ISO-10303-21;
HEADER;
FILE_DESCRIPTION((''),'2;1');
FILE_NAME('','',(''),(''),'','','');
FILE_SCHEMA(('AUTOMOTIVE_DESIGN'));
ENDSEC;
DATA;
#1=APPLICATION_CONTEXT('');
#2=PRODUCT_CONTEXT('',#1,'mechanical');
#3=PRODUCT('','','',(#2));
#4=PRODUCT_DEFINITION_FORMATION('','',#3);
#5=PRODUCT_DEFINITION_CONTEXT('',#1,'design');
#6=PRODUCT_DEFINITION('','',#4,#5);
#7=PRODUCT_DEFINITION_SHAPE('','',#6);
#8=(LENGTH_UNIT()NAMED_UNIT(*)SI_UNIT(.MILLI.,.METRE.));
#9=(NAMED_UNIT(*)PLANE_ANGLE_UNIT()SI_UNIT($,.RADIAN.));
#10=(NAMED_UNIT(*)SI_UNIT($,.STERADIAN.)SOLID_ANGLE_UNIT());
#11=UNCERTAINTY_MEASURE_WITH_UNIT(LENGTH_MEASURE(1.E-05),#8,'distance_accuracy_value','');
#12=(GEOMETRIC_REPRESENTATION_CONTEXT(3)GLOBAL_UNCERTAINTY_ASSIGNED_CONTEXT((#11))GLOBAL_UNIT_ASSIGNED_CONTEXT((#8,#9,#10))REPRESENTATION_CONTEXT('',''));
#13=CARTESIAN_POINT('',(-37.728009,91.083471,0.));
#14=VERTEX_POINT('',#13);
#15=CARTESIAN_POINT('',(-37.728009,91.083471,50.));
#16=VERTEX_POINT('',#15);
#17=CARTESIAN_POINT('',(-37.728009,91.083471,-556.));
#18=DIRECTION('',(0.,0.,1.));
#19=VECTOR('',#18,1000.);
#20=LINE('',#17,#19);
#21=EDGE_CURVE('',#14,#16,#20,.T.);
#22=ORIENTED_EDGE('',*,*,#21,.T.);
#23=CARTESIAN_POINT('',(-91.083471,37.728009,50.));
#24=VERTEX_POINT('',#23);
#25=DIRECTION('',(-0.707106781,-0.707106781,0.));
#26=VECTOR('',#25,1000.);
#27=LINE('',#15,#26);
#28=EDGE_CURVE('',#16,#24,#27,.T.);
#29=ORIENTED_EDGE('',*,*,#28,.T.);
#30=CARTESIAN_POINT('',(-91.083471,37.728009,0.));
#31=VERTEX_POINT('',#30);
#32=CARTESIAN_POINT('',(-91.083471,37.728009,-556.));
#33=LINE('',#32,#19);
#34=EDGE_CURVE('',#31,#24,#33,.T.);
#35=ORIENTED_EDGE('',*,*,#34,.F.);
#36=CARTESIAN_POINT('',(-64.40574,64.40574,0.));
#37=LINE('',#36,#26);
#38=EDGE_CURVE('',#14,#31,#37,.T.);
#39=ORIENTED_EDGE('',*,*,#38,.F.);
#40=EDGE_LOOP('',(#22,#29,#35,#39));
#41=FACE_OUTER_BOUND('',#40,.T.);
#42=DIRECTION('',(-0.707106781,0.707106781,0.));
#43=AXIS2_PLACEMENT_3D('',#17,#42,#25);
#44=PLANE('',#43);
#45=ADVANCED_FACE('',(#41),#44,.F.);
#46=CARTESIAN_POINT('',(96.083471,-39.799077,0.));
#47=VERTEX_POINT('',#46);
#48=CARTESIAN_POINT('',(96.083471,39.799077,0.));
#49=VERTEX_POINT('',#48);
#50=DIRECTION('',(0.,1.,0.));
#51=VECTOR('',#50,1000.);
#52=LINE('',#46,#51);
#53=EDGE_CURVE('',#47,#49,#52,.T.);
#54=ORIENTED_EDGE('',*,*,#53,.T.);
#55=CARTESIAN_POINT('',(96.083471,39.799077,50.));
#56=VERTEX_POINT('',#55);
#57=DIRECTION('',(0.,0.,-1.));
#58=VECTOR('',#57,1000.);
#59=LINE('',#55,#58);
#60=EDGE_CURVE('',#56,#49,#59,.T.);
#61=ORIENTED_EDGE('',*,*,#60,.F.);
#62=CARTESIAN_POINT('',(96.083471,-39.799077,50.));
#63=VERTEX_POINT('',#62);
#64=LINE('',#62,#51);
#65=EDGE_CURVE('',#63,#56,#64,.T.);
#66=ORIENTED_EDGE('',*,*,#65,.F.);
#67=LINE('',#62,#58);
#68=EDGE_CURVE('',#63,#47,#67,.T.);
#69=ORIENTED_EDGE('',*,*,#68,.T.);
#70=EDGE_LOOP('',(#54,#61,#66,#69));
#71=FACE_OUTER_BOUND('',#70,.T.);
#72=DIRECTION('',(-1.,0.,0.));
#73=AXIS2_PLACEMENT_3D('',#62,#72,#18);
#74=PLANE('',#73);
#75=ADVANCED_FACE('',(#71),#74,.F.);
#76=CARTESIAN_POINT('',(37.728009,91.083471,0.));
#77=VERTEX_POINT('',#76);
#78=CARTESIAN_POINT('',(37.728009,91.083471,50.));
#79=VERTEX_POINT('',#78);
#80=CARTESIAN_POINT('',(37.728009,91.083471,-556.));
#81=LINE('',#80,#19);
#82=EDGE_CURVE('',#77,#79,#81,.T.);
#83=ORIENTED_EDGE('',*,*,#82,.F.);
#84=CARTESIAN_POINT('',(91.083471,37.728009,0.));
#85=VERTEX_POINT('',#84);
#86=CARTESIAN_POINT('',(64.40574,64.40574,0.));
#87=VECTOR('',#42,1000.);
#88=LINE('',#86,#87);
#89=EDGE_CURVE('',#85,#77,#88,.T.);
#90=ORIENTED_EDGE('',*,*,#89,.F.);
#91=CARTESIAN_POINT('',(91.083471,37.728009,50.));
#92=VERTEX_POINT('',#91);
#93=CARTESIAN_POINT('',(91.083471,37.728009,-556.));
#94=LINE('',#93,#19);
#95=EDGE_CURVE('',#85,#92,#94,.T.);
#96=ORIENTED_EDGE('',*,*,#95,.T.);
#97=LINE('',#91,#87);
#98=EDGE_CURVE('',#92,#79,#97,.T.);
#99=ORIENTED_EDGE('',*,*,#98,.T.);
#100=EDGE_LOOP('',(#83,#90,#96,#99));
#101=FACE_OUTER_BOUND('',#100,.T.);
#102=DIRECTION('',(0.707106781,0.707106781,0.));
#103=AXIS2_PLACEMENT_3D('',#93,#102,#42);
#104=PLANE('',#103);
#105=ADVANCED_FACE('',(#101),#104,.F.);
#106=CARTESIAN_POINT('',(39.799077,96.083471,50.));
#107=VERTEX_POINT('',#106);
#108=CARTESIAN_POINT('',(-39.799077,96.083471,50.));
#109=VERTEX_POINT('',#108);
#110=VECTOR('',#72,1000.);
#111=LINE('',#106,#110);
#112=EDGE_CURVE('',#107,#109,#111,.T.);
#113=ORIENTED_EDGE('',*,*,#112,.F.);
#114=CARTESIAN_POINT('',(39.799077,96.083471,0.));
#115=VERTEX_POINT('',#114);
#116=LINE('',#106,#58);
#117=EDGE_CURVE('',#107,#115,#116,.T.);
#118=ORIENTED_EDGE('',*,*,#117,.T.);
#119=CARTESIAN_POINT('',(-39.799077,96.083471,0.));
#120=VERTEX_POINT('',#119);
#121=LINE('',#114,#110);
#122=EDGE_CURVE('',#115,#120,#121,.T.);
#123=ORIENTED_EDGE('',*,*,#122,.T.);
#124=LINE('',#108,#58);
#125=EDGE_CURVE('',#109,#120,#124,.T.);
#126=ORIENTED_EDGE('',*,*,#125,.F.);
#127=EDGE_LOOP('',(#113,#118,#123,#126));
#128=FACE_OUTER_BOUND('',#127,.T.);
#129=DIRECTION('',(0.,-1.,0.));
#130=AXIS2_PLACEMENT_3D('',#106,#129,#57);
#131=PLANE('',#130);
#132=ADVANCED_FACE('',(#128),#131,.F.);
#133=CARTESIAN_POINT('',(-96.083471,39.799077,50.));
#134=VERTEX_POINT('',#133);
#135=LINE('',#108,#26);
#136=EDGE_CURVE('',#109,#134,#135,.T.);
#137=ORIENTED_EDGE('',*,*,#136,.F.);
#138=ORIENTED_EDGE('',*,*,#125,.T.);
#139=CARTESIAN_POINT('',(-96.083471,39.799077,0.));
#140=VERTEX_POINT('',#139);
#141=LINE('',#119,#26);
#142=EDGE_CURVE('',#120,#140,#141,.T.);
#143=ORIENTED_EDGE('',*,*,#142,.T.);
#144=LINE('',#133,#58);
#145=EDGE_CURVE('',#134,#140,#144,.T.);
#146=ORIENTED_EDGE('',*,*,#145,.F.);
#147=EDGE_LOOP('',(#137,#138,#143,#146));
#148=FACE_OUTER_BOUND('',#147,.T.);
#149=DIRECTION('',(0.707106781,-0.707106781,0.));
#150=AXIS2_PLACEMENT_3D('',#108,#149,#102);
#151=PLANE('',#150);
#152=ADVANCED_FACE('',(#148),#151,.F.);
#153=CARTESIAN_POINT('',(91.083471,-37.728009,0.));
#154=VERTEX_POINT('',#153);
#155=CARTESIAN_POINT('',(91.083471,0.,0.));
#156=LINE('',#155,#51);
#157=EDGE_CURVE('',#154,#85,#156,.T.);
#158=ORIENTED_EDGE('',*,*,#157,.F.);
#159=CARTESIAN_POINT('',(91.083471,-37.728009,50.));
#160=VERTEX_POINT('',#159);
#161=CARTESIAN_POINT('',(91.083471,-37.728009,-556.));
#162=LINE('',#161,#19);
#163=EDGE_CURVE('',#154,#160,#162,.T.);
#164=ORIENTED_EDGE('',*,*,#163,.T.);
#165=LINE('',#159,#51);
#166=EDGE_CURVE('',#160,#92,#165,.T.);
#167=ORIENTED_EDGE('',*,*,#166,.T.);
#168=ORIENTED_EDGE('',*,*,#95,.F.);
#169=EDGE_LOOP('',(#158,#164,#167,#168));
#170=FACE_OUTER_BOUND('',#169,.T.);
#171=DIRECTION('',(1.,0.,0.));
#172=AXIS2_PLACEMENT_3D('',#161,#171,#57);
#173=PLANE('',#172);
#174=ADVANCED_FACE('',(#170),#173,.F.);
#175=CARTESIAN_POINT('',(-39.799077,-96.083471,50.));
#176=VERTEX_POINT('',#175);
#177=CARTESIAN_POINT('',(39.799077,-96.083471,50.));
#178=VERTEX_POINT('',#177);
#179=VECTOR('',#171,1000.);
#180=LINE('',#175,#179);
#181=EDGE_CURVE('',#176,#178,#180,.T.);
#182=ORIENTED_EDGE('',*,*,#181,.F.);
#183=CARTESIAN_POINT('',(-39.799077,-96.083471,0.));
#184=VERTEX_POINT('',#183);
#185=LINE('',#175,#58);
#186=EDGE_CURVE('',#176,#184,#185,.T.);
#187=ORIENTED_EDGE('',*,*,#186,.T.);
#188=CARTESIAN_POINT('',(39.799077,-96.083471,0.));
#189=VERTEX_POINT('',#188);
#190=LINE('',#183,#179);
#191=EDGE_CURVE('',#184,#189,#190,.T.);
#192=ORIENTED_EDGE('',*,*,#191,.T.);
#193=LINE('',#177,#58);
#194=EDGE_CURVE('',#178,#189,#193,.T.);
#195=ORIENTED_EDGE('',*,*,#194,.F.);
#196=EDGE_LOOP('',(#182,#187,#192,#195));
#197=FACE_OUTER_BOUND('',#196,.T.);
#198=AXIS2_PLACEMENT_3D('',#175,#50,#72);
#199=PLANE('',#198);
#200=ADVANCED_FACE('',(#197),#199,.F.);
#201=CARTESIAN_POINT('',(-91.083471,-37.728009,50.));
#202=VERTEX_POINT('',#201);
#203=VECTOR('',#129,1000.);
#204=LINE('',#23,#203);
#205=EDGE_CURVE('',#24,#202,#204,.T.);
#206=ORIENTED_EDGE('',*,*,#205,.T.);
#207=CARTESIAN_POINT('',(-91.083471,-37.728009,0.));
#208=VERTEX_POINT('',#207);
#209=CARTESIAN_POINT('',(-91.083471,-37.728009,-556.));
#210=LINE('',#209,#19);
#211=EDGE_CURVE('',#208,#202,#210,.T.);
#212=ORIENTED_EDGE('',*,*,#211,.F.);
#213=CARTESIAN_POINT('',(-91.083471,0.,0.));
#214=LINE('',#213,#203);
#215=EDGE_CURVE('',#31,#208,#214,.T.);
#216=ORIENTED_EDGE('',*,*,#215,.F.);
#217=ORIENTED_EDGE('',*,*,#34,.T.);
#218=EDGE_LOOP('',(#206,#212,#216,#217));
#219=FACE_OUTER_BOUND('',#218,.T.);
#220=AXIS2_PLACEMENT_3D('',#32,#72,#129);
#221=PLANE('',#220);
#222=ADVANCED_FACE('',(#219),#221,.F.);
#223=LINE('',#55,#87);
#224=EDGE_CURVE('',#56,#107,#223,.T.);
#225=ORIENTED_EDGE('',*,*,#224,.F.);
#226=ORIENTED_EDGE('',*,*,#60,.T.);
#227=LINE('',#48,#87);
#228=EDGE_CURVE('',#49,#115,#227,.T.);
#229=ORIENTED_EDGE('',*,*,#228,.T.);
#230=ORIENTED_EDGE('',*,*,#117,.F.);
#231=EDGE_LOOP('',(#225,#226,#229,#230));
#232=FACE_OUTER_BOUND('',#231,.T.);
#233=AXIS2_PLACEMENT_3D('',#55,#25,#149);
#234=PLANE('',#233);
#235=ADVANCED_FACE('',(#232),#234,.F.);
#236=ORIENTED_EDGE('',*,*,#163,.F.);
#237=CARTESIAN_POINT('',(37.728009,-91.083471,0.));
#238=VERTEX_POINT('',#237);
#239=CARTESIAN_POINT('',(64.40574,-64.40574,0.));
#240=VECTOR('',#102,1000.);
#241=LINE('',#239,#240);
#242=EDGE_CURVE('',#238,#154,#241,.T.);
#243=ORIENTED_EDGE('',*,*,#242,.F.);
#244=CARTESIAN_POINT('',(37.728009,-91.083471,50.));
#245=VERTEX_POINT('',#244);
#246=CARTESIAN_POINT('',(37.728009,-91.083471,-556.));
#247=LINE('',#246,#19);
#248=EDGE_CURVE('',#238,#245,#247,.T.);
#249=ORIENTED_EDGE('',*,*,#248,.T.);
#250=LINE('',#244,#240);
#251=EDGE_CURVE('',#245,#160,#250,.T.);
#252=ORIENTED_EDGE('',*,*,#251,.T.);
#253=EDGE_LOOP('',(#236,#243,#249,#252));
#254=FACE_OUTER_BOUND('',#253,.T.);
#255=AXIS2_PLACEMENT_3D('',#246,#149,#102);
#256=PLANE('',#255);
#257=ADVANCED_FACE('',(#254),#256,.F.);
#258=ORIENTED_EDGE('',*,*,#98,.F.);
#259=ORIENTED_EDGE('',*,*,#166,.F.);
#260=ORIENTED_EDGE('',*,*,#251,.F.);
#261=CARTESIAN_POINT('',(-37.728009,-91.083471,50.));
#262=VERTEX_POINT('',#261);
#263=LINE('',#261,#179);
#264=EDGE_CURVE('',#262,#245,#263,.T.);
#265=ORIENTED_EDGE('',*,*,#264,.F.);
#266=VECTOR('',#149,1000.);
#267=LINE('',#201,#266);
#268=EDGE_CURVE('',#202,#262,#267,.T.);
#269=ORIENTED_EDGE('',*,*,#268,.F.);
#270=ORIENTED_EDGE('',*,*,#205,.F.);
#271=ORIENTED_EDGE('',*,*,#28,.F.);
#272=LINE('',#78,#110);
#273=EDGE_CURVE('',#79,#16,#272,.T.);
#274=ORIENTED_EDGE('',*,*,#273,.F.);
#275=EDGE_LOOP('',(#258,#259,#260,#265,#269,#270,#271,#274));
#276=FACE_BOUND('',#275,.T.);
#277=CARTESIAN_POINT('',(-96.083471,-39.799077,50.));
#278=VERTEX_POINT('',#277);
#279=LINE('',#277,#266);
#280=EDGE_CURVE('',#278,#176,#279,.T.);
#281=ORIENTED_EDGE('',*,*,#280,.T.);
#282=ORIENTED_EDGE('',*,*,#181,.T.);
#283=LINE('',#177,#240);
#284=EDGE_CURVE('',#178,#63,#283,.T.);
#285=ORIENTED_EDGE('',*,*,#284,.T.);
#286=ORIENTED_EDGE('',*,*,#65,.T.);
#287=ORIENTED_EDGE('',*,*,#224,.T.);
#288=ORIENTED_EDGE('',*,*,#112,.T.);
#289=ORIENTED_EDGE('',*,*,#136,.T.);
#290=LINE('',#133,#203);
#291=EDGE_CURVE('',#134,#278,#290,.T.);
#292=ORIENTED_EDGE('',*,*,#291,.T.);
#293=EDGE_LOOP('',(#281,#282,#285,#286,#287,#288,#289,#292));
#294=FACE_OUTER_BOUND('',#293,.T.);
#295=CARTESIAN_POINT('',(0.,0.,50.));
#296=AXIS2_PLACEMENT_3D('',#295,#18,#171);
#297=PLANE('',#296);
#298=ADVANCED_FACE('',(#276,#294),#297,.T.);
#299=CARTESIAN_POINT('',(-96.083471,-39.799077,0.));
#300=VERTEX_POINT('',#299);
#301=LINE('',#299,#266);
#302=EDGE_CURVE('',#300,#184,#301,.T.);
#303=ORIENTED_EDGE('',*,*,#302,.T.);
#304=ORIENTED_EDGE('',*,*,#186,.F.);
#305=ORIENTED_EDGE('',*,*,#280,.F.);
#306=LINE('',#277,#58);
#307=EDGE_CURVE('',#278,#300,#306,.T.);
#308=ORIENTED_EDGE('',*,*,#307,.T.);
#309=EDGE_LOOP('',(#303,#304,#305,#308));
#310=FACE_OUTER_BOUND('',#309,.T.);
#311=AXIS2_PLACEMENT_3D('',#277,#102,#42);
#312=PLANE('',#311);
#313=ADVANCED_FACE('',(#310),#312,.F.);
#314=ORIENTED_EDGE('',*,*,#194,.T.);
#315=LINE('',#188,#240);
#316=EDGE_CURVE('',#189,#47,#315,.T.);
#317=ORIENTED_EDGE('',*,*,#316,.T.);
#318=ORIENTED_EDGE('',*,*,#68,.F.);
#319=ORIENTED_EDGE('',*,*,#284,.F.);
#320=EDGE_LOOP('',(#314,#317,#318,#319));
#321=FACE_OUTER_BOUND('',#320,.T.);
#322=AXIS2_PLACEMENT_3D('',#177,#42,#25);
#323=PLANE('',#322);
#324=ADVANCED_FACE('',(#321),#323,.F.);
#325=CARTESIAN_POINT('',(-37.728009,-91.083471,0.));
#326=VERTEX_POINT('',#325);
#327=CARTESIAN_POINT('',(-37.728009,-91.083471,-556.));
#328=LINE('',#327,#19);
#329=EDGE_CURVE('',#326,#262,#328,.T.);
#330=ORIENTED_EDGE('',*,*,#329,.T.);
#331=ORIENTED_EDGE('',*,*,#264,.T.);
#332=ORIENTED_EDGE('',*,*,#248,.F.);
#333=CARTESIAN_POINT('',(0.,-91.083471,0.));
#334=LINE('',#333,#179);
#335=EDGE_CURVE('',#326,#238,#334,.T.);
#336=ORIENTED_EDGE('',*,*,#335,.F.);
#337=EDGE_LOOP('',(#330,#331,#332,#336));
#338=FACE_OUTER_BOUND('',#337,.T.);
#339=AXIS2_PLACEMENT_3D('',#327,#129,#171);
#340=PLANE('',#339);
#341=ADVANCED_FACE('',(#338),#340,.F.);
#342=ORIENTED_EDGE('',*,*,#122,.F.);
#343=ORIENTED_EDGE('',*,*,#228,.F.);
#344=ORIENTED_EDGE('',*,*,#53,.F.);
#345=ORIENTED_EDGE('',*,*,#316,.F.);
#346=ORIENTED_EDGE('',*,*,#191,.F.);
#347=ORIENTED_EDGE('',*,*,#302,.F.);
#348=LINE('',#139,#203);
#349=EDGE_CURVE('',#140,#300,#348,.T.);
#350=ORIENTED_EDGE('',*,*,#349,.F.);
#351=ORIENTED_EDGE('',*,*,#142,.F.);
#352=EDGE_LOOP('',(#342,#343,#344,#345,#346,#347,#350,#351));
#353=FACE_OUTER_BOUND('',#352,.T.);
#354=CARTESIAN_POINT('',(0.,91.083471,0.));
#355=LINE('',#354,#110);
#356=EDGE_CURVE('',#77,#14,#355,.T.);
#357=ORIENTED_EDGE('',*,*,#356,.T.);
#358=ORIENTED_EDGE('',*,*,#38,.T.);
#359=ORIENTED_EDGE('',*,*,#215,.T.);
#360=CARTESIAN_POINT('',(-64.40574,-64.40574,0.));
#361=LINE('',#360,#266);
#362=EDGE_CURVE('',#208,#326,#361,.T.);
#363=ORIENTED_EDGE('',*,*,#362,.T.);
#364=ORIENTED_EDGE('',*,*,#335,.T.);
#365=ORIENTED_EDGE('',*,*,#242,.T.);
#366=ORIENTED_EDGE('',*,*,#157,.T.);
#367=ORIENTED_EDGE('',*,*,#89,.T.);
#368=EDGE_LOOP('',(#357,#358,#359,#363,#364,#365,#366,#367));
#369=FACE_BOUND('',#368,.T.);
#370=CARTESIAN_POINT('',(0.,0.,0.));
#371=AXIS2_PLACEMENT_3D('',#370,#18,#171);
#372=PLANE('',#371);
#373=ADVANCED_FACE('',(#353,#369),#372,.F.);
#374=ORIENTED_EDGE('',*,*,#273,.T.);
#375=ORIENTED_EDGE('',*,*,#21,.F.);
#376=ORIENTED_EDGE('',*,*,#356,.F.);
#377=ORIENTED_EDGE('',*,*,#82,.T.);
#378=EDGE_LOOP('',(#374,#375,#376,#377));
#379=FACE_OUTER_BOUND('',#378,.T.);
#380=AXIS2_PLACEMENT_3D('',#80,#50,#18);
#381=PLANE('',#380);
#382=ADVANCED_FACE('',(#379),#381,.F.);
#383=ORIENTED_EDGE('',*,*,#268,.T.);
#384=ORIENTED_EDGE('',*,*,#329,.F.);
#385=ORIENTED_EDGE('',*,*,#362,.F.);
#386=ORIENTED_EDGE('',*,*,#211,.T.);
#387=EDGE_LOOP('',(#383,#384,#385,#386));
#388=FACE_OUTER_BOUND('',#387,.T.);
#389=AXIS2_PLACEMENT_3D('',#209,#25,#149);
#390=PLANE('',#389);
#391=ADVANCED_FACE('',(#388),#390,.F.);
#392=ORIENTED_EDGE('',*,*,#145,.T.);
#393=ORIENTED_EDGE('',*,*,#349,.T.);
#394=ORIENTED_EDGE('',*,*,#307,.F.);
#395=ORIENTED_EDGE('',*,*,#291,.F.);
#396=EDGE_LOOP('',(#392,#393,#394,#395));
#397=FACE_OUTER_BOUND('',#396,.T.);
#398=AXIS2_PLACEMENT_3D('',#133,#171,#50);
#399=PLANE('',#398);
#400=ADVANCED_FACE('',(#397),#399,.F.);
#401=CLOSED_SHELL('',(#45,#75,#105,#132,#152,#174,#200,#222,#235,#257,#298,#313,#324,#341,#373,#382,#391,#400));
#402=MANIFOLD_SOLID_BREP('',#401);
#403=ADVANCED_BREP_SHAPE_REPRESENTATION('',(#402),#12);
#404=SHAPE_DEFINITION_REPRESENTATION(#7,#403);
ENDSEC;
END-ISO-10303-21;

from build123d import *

# Parameters (mm, degrees)
EXTRUDE_1_DEPTH     = 50
CUT_EXTRUDE_1_DEPTH = 606


with BuildPart() as part:
    # 草图1 → 凸台-拉伸1 (new body)
    with BuildSketch(Plane.XY):
        Polygon((-39.799076966, 96.083471381), (-96.083471381, 39.799076966), (-96.083471381, -39.799076966), (-39.799076966, -96.083471381), (39.799076966, -96.083471381), (96.083471381, -39.799076966), (96.083471381, 39.799076966), (39.799076966, 96.083471381), align=None)
    extrude(amount=EXTRUDE_1_DEPTH)

    # 草图2 → 切除-拉伸1 (cut)
    with BuildSketch(Plane.XY.offset(50)):
        Polygon((37.728009154, 91.083471381), (-37.728009154, 91.083471381), (-91.083471381, 37.728009154), (-91.083471381, -37.728009154), (-37.728009154, -91.083471381), (37.728009154, -91.083471381), (91.083471381, -37.728009154), (91.083471381, 37.728009154), align=None)
    extrude(amount=-CUT_EXTRUDE_1_DEPTH, mode=Mode.SUBTRACT)


solid = part.part
